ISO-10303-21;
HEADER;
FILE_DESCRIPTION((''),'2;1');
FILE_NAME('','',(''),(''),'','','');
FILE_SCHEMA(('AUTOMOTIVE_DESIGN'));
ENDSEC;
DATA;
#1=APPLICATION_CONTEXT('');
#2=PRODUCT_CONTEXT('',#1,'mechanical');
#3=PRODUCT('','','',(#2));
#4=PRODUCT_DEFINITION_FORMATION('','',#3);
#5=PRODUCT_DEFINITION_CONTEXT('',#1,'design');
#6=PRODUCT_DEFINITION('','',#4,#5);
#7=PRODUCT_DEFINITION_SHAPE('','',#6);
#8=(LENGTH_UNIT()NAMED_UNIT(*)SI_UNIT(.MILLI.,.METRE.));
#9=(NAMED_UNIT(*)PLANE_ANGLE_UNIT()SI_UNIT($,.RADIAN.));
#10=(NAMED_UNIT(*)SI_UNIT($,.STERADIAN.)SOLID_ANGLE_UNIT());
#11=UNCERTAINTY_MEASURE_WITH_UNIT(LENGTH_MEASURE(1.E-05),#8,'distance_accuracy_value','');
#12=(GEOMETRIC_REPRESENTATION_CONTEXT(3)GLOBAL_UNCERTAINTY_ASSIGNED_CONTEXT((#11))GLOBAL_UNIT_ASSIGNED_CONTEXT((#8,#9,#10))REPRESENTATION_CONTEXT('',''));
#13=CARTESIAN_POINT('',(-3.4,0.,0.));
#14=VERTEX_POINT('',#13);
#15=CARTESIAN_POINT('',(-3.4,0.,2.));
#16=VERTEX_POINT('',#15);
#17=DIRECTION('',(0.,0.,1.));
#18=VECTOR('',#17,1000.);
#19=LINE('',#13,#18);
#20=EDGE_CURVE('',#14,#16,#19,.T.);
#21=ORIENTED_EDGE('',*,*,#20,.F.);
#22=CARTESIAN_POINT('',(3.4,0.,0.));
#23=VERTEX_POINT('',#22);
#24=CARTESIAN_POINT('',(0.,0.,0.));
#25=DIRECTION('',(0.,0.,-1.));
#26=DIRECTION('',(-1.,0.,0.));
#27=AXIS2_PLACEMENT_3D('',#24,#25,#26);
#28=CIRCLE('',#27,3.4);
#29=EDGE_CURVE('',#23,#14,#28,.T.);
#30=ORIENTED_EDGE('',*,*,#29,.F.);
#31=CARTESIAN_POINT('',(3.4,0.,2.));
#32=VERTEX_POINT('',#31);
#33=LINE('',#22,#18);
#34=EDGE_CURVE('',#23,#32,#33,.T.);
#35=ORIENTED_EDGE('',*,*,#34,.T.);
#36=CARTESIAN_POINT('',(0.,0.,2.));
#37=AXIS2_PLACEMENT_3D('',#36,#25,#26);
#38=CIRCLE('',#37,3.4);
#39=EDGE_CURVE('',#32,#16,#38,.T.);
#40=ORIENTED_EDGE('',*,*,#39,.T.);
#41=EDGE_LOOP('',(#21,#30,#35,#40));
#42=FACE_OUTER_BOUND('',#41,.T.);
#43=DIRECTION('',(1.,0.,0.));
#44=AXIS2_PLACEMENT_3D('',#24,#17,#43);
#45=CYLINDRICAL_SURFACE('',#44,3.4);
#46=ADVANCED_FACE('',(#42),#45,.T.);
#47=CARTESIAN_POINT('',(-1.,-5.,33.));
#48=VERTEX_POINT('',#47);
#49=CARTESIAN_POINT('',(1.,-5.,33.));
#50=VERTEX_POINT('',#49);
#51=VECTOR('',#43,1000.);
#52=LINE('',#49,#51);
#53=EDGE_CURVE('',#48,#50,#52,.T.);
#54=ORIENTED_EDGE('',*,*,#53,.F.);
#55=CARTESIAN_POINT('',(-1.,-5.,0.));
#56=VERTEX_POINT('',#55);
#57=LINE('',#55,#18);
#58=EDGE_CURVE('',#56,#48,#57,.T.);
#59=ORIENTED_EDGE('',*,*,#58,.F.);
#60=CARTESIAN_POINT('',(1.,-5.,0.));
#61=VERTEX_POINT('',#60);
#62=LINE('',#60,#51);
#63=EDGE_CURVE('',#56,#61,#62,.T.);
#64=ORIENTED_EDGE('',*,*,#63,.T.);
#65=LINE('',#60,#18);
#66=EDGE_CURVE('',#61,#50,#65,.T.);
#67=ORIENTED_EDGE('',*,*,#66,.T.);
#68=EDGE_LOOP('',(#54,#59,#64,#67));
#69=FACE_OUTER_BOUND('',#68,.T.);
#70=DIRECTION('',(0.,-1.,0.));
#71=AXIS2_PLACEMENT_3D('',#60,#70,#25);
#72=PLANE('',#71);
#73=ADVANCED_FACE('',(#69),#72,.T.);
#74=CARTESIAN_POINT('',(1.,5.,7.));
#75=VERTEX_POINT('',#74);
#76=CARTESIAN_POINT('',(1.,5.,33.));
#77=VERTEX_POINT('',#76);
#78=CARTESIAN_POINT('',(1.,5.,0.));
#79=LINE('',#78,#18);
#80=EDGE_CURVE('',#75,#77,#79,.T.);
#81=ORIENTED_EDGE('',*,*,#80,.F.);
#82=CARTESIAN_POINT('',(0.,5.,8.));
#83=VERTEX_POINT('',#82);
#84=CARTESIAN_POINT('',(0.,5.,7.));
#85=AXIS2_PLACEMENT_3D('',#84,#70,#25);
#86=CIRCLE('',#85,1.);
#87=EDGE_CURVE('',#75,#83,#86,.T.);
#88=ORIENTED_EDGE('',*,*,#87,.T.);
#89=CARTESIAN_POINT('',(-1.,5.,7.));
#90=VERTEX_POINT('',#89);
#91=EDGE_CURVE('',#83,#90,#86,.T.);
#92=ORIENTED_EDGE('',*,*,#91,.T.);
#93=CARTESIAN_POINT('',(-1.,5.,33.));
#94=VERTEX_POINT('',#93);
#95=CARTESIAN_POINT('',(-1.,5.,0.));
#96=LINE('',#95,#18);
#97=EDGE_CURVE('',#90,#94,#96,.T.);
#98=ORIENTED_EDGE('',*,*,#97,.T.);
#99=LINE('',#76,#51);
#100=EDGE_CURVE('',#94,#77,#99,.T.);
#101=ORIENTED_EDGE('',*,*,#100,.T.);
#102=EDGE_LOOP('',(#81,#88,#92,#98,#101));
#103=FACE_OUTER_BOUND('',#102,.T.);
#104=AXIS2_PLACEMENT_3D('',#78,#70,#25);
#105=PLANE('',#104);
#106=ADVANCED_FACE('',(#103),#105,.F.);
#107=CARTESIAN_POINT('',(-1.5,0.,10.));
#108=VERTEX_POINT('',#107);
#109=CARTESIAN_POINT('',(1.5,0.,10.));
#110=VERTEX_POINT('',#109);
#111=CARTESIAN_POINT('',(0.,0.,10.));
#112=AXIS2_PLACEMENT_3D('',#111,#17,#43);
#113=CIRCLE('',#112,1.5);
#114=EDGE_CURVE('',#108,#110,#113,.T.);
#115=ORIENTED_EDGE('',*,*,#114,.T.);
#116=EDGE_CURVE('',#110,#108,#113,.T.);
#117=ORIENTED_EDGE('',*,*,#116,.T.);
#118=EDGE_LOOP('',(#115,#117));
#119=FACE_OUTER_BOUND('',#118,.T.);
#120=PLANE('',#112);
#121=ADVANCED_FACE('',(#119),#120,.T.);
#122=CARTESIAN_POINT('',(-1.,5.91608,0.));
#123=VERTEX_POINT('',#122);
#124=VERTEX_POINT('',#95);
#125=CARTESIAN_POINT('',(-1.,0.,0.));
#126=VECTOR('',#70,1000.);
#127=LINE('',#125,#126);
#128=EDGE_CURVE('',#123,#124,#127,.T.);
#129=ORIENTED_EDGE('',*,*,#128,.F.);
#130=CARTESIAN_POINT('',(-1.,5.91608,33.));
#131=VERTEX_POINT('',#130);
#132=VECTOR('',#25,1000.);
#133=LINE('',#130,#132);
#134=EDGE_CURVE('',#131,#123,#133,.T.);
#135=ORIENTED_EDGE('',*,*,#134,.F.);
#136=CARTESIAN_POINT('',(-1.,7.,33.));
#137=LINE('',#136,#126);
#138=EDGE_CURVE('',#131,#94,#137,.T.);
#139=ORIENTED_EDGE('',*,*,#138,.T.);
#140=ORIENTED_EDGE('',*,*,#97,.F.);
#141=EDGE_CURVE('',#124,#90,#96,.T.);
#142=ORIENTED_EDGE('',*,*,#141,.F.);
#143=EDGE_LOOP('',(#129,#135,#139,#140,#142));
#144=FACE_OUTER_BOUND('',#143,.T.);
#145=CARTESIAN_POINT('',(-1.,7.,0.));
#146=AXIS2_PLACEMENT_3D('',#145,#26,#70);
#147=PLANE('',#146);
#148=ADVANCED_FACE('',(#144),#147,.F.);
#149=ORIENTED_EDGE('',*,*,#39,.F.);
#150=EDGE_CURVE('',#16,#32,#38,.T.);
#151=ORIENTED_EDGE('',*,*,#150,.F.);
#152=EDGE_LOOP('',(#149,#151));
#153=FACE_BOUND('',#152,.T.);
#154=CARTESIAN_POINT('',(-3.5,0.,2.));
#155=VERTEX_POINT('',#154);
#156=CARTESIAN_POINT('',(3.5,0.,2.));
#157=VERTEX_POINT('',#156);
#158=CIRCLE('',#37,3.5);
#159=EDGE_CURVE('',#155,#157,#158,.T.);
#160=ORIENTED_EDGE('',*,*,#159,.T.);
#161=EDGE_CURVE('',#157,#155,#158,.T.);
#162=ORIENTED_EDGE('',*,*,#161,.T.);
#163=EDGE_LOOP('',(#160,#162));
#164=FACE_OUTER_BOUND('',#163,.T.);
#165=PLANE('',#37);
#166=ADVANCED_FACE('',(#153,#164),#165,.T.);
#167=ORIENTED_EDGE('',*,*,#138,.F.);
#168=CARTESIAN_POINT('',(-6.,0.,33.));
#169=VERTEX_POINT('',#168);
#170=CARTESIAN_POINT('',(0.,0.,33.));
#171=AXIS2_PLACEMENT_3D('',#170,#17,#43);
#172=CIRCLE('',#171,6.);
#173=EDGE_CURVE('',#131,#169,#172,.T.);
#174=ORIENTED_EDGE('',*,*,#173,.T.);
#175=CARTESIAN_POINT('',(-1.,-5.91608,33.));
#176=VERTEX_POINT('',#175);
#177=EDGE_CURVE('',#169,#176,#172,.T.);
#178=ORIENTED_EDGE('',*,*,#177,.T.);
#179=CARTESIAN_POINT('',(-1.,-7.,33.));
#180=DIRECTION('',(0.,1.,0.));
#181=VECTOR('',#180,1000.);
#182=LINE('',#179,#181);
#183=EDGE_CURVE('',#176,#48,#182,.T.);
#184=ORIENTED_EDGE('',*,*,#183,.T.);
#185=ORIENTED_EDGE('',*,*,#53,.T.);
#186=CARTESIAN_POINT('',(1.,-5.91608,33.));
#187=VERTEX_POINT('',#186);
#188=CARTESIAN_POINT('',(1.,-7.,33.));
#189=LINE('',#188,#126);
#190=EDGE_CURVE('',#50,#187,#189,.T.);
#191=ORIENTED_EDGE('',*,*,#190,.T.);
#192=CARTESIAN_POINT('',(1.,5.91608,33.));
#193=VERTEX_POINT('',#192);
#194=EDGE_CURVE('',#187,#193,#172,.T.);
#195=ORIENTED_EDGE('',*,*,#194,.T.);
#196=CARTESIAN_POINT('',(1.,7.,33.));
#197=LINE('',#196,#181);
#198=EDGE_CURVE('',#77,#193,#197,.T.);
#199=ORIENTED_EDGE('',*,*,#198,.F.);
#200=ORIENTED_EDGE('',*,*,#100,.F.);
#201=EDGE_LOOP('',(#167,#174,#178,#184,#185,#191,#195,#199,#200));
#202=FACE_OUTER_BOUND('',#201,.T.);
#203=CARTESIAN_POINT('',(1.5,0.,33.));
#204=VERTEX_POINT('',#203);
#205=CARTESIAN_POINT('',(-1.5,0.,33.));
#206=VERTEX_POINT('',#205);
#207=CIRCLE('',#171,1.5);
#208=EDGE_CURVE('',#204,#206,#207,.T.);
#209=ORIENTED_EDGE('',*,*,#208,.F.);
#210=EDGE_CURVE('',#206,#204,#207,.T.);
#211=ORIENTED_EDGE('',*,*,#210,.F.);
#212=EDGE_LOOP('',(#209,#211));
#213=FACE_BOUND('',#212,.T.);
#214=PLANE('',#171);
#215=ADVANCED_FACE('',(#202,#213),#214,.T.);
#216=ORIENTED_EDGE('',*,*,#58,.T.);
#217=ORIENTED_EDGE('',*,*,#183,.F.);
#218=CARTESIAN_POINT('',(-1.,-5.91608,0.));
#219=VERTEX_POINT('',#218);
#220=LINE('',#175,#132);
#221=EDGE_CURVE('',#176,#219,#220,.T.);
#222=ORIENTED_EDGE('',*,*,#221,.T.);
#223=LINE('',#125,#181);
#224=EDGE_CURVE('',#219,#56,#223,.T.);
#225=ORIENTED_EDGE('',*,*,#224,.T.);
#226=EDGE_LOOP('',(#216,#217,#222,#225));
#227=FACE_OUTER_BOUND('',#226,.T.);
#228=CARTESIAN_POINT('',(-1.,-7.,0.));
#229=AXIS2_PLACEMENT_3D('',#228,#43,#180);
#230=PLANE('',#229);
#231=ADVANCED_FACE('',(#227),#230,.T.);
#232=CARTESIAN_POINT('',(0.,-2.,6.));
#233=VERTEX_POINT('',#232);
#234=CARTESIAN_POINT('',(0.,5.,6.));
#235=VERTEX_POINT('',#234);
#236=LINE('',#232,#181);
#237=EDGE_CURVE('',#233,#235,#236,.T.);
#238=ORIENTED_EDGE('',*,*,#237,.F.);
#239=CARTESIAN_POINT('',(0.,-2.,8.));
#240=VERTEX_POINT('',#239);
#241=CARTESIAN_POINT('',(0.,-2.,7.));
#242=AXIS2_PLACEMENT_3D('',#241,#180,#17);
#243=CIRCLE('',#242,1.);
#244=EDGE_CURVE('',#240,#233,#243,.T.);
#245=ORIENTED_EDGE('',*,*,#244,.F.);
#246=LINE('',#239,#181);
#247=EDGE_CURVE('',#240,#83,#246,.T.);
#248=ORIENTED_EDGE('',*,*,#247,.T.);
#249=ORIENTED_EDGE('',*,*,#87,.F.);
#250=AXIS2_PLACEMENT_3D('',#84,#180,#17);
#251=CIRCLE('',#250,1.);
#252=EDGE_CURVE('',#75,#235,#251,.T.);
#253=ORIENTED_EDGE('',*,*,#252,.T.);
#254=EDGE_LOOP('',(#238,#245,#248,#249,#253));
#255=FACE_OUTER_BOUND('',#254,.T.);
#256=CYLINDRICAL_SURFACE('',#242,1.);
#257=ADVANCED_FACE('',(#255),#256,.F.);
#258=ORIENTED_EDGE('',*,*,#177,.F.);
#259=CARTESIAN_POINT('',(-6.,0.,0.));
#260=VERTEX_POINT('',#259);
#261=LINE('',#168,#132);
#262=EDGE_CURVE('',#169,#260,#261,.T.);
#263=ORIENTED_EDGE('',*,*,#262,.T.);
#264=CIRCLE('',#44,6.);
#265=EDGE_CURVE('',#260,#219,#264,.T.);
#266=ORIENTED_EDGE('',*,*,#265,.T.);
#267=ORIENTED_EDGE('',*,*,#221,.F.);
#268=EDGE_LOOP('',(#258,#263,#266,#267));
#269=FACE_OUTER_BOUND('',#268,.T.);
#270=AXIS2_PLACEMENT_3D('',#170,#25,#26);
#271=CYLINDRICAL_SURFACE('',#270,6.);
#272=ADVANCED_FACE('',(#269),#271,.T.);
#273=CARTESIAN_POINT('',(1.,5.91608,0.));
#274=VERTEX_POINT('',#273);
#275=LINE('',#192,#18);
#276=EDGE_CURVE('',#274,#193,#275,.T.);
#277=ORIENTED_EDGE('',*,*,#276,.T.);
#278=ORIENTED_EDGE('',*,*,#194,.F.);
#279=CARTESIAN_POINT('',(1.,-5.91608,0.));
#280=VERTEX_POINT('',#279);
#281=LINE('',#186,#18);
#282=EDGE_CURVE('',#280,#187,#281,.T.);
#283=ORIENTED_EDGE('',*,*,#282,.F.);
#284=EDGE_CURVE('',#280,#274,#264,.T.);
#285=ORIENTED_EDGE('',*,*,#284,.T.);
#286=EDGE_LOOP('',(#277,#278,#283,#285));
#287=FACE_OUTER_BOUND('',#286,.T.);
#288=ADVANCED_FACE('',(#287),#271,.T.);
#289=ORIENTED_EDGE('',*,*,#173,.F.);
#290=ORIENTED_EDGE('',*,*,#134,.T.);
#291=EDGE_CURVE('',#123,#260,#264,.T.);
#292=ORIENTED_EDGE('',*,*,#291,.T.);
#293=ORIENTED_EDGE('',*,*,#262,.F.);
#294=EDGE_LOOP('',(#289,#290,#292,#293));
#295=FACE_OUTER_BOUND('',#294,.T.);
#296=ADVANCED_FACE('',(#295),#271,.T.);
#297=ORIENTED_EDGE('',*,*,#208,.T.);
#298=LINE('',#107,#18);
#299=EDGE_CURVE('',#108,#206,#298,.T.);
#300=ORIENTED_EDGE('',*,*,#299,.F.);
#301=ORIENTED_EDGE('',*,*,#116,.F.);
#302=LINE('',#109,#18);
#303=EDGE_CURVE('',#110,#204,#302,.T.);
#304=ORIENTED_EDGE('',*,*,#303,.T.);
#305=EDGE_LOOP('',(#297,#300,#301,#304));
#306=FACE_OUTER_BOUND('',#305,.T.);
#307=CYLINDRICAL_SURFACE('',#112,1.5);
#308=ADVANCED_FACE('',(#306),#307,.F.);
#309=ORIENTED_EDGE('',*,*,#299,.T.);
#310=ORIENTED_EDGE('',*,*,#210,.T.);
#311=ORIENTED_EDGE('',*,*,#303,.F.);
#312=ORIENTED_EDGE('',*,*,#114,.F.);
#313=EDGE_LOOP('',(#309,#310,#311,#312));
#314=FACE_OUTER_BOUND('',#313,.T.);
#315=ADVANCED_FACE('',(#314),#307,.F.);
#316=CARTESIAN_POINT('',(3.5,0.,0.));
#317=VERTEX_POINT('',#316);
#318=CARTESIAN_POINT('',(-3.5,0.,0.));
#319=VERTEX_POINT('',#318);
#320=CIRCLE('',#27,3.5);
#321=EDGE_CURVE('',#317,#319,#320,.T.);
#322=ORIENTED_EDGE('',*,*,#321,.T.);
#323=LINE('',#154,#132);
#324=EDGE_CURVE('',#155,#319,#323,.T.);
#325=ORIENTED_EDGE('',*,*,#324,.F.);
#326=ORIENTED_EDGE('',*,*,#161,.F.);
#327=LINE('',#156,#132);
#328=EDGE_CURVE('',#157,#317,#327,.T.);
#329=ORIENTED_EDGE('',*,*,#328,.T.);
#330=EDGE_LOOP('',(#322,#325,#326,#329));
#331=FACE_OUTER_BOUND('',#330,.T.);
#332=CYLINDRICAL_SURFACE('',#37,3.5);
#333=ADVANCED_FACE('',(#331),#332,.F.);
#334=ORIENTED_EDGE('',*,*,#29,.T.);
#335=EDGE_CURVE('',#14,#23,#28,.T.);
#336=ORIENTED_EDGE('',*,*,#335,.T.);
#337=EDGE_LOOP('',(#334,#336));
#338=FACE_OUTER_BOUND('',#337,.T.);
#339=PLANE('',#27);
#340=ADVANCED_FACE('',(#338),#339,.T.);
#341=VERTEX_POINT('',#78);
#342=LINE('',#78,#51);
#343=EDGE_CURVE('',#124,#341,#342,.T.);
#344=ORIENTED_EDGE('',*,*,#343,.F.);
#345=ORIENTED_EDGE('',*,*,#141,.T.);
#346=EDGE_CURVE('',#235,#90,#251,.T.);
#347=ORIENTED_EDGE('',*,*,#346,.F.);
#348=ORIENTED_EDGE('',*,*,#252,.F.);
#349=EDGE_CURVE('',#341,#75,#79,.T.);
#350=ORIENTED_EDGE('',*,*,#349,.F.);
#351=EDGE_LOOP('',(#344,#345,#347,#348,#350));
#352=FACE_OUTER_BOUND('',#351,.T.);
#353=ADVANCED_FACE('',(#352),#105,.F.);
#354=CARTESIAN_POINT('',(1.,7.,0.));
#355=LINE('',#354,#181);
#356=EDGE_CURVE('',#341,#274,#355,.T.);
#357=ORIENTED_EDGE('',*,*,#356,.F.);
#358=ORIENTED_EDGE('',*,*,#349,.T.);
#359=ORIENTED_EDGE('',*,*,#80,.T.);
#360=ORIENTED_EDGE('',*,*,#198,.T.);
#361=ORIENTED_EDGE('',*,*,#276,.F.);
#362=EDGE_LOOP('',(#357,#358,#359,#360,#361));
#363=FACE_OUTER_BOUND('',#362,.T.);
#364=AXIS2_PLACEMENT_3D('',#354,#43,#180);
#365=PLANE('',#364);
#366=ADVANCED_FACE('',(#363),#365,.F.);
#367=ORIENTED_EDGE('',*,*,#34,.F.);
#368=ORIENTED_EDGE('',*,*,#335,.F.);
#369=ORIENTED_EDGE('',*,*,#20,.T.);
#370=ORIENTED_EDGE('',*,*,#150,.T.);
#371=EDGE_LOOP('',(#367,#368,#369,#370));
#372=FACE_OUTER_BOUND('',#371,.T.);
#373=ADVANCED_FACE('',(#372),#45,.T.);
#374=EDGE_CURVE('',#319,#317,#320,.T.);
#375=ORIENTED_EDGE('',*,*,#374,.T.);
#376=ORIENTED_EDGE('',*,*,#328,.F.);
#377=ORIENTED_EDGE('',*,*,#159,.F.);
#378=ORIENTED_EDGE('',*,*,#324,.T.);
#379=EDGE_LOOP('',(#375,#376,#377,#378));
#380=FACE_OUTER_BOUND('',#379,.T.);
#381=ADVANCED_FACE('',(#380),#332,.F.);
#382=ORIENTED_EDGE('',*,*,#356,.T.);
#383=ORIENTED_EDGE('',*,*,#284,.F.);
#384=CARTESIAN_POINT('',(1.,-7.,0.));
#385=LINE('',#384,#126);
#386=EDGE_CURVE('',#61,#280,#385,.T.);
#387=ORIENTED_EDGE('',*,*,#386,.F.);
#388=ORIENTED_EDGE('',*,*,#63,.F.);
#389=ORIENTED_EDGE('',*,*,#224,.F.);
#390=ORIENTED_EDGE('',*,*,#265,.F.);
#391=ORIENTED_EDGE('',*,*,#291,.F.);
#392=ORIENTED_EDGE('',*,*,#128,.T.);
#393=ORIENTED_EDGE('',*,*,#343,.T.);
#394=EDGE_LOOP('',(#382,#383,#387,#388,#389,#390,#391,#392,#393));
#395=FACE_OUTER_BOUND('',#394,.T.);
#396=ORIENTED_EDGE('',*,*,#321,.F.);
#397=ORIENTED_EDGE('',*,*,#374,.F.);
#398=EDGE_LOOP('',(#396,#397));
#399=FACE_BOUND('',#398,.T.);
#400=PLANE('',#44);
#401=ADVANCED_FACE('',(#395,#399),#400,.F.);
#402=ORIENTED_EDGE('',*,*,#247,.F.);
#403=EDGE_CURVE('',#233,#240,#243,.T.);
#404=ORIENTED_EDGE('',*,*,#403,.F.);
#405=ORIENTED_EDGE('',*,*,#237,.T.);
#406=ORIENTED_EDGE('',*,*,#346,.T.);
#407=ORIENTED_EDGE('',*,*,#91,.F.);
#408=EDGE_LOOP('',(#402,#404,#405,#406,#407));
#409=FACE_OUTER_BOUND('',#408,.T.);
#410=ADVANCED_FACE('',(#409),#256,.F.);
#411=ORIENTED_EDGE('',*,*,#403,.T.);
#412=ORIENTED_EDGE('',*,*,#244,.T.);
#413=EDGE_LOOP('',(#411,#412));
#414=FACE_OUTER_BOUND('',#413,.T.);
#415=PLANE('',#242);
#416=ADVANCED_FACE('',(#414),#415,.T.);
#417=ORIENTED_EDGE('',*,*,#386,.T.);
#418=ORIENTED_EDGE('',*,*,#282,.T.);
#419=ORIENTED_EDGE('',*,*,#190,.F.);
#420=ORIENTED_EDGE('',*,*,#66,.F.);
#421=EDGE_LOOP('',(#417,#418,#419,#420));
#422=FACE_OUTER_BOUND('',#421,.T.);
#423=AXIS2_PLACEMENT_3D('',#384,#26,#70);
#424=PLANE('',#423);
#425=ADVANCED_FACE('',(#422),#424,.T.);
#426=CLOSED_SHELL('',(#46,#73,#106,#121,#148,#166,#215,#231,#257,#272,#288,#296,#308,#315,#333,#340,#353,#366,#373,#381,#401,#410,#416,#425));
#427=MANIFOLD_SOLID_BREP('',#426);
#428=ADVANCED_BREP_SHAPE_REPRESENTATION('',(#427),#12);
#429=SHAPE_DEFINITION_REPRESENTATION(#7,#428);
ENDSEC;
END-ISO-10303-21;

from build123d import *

# Parameters (mm, degrees)
SKETCH1_R           = 6
BOSS_EXTRUDE1_DEPTH = 33
SKETCH2_W           = 2
SKETCH2_H           = 2
CUT_EXTRUDE1_DEPTH  = 33
SKETCH3_R           = 1.5
CUT_EXTRUDE2_DEPTH  = 23
SKETCH4_R           = 1
CUT_EXTRUDE3_DEPTH  = 7
SKETCH5_R           = 3.5
CUT_EXTRUDE4_DEPTH  = 2
SKETCH6_R           = 3.4
BOSS_EXTRUDE2_DEPTH = 2


with BuildPart() as part:
    # Sketch1 → Boss-Extrude1 (new body)
    with BuildSketch(Plane.XY):
        Circle(SKETCH1_R)
    extrude(amount=BOSS_EXTRUDE1_DEPTH)

    # Sketch2 → Cut-Extrude1 (cut)
    with BuildSketch(Plane.XY.offset(33)):
        with Locations((0, 6)):
            Rectangle(SKETCH2_W, SKETCH2_H)
    cut_extrude1 = extrude(amount=-CUT_EXTRUDE1_DEPTH, mode=Mode.SUBTRACT)

    # Mirror1: Cut-Extrude1 across plane
    add(cut_extrude1.mirror(Plane.ZX), mode=Mode.SUBTRACT)

    # Sketch3 → Cut-Extrude2 (cut)
    with BuildSketch(Plane.XY.offset(33)):
        Circle(SKETCH3_R)
    extrude(amount=-CUT_EXTRUDE2_DEPTH, mode=Mode.SUBTRACT)

    # Sketch4 → Cut-Extrude3 (cut)
    with BuildSketch(Plane(origin=(0, 5, 0), x_dir=(1, 0, 0), z_dir=(0, 1, 0))):
        with Locations(Location((0, -7, 0), (0, 0, 270))):
            Circle(SKETCH4_R)
    extrude(amount=-CUT_EXTRUDE3_DEPTH, mode=Mode.SUBTRACT)

    # Sketch5 → Cut-Extrude4 (cut)
    with BuildSketch(Plane(origin=(0, 0, 0), x_dir=(-1, 0, 0), z_dir=(0, 0, -1))):
        Circle(SKETCH5_R)
    extrude(amount=-CUT_EXTRUDE4_DEPTH, mode=Mode.SUBTRACT)

    # Sketch6 → Boss-Extrude2 (add)
    with BuildSketch(Plane(origin=(0, 0, 2), x_dir=(-1, 0, 0), z_dir=(0, 0, -1))):
        with Locations(Location((0, 0, 0), (0, 0, 180))):
            Circle(SKETCH6_R)
    extrude(amount=BOSS_EXTRUDE2_DEPTH)


solid = part.part
